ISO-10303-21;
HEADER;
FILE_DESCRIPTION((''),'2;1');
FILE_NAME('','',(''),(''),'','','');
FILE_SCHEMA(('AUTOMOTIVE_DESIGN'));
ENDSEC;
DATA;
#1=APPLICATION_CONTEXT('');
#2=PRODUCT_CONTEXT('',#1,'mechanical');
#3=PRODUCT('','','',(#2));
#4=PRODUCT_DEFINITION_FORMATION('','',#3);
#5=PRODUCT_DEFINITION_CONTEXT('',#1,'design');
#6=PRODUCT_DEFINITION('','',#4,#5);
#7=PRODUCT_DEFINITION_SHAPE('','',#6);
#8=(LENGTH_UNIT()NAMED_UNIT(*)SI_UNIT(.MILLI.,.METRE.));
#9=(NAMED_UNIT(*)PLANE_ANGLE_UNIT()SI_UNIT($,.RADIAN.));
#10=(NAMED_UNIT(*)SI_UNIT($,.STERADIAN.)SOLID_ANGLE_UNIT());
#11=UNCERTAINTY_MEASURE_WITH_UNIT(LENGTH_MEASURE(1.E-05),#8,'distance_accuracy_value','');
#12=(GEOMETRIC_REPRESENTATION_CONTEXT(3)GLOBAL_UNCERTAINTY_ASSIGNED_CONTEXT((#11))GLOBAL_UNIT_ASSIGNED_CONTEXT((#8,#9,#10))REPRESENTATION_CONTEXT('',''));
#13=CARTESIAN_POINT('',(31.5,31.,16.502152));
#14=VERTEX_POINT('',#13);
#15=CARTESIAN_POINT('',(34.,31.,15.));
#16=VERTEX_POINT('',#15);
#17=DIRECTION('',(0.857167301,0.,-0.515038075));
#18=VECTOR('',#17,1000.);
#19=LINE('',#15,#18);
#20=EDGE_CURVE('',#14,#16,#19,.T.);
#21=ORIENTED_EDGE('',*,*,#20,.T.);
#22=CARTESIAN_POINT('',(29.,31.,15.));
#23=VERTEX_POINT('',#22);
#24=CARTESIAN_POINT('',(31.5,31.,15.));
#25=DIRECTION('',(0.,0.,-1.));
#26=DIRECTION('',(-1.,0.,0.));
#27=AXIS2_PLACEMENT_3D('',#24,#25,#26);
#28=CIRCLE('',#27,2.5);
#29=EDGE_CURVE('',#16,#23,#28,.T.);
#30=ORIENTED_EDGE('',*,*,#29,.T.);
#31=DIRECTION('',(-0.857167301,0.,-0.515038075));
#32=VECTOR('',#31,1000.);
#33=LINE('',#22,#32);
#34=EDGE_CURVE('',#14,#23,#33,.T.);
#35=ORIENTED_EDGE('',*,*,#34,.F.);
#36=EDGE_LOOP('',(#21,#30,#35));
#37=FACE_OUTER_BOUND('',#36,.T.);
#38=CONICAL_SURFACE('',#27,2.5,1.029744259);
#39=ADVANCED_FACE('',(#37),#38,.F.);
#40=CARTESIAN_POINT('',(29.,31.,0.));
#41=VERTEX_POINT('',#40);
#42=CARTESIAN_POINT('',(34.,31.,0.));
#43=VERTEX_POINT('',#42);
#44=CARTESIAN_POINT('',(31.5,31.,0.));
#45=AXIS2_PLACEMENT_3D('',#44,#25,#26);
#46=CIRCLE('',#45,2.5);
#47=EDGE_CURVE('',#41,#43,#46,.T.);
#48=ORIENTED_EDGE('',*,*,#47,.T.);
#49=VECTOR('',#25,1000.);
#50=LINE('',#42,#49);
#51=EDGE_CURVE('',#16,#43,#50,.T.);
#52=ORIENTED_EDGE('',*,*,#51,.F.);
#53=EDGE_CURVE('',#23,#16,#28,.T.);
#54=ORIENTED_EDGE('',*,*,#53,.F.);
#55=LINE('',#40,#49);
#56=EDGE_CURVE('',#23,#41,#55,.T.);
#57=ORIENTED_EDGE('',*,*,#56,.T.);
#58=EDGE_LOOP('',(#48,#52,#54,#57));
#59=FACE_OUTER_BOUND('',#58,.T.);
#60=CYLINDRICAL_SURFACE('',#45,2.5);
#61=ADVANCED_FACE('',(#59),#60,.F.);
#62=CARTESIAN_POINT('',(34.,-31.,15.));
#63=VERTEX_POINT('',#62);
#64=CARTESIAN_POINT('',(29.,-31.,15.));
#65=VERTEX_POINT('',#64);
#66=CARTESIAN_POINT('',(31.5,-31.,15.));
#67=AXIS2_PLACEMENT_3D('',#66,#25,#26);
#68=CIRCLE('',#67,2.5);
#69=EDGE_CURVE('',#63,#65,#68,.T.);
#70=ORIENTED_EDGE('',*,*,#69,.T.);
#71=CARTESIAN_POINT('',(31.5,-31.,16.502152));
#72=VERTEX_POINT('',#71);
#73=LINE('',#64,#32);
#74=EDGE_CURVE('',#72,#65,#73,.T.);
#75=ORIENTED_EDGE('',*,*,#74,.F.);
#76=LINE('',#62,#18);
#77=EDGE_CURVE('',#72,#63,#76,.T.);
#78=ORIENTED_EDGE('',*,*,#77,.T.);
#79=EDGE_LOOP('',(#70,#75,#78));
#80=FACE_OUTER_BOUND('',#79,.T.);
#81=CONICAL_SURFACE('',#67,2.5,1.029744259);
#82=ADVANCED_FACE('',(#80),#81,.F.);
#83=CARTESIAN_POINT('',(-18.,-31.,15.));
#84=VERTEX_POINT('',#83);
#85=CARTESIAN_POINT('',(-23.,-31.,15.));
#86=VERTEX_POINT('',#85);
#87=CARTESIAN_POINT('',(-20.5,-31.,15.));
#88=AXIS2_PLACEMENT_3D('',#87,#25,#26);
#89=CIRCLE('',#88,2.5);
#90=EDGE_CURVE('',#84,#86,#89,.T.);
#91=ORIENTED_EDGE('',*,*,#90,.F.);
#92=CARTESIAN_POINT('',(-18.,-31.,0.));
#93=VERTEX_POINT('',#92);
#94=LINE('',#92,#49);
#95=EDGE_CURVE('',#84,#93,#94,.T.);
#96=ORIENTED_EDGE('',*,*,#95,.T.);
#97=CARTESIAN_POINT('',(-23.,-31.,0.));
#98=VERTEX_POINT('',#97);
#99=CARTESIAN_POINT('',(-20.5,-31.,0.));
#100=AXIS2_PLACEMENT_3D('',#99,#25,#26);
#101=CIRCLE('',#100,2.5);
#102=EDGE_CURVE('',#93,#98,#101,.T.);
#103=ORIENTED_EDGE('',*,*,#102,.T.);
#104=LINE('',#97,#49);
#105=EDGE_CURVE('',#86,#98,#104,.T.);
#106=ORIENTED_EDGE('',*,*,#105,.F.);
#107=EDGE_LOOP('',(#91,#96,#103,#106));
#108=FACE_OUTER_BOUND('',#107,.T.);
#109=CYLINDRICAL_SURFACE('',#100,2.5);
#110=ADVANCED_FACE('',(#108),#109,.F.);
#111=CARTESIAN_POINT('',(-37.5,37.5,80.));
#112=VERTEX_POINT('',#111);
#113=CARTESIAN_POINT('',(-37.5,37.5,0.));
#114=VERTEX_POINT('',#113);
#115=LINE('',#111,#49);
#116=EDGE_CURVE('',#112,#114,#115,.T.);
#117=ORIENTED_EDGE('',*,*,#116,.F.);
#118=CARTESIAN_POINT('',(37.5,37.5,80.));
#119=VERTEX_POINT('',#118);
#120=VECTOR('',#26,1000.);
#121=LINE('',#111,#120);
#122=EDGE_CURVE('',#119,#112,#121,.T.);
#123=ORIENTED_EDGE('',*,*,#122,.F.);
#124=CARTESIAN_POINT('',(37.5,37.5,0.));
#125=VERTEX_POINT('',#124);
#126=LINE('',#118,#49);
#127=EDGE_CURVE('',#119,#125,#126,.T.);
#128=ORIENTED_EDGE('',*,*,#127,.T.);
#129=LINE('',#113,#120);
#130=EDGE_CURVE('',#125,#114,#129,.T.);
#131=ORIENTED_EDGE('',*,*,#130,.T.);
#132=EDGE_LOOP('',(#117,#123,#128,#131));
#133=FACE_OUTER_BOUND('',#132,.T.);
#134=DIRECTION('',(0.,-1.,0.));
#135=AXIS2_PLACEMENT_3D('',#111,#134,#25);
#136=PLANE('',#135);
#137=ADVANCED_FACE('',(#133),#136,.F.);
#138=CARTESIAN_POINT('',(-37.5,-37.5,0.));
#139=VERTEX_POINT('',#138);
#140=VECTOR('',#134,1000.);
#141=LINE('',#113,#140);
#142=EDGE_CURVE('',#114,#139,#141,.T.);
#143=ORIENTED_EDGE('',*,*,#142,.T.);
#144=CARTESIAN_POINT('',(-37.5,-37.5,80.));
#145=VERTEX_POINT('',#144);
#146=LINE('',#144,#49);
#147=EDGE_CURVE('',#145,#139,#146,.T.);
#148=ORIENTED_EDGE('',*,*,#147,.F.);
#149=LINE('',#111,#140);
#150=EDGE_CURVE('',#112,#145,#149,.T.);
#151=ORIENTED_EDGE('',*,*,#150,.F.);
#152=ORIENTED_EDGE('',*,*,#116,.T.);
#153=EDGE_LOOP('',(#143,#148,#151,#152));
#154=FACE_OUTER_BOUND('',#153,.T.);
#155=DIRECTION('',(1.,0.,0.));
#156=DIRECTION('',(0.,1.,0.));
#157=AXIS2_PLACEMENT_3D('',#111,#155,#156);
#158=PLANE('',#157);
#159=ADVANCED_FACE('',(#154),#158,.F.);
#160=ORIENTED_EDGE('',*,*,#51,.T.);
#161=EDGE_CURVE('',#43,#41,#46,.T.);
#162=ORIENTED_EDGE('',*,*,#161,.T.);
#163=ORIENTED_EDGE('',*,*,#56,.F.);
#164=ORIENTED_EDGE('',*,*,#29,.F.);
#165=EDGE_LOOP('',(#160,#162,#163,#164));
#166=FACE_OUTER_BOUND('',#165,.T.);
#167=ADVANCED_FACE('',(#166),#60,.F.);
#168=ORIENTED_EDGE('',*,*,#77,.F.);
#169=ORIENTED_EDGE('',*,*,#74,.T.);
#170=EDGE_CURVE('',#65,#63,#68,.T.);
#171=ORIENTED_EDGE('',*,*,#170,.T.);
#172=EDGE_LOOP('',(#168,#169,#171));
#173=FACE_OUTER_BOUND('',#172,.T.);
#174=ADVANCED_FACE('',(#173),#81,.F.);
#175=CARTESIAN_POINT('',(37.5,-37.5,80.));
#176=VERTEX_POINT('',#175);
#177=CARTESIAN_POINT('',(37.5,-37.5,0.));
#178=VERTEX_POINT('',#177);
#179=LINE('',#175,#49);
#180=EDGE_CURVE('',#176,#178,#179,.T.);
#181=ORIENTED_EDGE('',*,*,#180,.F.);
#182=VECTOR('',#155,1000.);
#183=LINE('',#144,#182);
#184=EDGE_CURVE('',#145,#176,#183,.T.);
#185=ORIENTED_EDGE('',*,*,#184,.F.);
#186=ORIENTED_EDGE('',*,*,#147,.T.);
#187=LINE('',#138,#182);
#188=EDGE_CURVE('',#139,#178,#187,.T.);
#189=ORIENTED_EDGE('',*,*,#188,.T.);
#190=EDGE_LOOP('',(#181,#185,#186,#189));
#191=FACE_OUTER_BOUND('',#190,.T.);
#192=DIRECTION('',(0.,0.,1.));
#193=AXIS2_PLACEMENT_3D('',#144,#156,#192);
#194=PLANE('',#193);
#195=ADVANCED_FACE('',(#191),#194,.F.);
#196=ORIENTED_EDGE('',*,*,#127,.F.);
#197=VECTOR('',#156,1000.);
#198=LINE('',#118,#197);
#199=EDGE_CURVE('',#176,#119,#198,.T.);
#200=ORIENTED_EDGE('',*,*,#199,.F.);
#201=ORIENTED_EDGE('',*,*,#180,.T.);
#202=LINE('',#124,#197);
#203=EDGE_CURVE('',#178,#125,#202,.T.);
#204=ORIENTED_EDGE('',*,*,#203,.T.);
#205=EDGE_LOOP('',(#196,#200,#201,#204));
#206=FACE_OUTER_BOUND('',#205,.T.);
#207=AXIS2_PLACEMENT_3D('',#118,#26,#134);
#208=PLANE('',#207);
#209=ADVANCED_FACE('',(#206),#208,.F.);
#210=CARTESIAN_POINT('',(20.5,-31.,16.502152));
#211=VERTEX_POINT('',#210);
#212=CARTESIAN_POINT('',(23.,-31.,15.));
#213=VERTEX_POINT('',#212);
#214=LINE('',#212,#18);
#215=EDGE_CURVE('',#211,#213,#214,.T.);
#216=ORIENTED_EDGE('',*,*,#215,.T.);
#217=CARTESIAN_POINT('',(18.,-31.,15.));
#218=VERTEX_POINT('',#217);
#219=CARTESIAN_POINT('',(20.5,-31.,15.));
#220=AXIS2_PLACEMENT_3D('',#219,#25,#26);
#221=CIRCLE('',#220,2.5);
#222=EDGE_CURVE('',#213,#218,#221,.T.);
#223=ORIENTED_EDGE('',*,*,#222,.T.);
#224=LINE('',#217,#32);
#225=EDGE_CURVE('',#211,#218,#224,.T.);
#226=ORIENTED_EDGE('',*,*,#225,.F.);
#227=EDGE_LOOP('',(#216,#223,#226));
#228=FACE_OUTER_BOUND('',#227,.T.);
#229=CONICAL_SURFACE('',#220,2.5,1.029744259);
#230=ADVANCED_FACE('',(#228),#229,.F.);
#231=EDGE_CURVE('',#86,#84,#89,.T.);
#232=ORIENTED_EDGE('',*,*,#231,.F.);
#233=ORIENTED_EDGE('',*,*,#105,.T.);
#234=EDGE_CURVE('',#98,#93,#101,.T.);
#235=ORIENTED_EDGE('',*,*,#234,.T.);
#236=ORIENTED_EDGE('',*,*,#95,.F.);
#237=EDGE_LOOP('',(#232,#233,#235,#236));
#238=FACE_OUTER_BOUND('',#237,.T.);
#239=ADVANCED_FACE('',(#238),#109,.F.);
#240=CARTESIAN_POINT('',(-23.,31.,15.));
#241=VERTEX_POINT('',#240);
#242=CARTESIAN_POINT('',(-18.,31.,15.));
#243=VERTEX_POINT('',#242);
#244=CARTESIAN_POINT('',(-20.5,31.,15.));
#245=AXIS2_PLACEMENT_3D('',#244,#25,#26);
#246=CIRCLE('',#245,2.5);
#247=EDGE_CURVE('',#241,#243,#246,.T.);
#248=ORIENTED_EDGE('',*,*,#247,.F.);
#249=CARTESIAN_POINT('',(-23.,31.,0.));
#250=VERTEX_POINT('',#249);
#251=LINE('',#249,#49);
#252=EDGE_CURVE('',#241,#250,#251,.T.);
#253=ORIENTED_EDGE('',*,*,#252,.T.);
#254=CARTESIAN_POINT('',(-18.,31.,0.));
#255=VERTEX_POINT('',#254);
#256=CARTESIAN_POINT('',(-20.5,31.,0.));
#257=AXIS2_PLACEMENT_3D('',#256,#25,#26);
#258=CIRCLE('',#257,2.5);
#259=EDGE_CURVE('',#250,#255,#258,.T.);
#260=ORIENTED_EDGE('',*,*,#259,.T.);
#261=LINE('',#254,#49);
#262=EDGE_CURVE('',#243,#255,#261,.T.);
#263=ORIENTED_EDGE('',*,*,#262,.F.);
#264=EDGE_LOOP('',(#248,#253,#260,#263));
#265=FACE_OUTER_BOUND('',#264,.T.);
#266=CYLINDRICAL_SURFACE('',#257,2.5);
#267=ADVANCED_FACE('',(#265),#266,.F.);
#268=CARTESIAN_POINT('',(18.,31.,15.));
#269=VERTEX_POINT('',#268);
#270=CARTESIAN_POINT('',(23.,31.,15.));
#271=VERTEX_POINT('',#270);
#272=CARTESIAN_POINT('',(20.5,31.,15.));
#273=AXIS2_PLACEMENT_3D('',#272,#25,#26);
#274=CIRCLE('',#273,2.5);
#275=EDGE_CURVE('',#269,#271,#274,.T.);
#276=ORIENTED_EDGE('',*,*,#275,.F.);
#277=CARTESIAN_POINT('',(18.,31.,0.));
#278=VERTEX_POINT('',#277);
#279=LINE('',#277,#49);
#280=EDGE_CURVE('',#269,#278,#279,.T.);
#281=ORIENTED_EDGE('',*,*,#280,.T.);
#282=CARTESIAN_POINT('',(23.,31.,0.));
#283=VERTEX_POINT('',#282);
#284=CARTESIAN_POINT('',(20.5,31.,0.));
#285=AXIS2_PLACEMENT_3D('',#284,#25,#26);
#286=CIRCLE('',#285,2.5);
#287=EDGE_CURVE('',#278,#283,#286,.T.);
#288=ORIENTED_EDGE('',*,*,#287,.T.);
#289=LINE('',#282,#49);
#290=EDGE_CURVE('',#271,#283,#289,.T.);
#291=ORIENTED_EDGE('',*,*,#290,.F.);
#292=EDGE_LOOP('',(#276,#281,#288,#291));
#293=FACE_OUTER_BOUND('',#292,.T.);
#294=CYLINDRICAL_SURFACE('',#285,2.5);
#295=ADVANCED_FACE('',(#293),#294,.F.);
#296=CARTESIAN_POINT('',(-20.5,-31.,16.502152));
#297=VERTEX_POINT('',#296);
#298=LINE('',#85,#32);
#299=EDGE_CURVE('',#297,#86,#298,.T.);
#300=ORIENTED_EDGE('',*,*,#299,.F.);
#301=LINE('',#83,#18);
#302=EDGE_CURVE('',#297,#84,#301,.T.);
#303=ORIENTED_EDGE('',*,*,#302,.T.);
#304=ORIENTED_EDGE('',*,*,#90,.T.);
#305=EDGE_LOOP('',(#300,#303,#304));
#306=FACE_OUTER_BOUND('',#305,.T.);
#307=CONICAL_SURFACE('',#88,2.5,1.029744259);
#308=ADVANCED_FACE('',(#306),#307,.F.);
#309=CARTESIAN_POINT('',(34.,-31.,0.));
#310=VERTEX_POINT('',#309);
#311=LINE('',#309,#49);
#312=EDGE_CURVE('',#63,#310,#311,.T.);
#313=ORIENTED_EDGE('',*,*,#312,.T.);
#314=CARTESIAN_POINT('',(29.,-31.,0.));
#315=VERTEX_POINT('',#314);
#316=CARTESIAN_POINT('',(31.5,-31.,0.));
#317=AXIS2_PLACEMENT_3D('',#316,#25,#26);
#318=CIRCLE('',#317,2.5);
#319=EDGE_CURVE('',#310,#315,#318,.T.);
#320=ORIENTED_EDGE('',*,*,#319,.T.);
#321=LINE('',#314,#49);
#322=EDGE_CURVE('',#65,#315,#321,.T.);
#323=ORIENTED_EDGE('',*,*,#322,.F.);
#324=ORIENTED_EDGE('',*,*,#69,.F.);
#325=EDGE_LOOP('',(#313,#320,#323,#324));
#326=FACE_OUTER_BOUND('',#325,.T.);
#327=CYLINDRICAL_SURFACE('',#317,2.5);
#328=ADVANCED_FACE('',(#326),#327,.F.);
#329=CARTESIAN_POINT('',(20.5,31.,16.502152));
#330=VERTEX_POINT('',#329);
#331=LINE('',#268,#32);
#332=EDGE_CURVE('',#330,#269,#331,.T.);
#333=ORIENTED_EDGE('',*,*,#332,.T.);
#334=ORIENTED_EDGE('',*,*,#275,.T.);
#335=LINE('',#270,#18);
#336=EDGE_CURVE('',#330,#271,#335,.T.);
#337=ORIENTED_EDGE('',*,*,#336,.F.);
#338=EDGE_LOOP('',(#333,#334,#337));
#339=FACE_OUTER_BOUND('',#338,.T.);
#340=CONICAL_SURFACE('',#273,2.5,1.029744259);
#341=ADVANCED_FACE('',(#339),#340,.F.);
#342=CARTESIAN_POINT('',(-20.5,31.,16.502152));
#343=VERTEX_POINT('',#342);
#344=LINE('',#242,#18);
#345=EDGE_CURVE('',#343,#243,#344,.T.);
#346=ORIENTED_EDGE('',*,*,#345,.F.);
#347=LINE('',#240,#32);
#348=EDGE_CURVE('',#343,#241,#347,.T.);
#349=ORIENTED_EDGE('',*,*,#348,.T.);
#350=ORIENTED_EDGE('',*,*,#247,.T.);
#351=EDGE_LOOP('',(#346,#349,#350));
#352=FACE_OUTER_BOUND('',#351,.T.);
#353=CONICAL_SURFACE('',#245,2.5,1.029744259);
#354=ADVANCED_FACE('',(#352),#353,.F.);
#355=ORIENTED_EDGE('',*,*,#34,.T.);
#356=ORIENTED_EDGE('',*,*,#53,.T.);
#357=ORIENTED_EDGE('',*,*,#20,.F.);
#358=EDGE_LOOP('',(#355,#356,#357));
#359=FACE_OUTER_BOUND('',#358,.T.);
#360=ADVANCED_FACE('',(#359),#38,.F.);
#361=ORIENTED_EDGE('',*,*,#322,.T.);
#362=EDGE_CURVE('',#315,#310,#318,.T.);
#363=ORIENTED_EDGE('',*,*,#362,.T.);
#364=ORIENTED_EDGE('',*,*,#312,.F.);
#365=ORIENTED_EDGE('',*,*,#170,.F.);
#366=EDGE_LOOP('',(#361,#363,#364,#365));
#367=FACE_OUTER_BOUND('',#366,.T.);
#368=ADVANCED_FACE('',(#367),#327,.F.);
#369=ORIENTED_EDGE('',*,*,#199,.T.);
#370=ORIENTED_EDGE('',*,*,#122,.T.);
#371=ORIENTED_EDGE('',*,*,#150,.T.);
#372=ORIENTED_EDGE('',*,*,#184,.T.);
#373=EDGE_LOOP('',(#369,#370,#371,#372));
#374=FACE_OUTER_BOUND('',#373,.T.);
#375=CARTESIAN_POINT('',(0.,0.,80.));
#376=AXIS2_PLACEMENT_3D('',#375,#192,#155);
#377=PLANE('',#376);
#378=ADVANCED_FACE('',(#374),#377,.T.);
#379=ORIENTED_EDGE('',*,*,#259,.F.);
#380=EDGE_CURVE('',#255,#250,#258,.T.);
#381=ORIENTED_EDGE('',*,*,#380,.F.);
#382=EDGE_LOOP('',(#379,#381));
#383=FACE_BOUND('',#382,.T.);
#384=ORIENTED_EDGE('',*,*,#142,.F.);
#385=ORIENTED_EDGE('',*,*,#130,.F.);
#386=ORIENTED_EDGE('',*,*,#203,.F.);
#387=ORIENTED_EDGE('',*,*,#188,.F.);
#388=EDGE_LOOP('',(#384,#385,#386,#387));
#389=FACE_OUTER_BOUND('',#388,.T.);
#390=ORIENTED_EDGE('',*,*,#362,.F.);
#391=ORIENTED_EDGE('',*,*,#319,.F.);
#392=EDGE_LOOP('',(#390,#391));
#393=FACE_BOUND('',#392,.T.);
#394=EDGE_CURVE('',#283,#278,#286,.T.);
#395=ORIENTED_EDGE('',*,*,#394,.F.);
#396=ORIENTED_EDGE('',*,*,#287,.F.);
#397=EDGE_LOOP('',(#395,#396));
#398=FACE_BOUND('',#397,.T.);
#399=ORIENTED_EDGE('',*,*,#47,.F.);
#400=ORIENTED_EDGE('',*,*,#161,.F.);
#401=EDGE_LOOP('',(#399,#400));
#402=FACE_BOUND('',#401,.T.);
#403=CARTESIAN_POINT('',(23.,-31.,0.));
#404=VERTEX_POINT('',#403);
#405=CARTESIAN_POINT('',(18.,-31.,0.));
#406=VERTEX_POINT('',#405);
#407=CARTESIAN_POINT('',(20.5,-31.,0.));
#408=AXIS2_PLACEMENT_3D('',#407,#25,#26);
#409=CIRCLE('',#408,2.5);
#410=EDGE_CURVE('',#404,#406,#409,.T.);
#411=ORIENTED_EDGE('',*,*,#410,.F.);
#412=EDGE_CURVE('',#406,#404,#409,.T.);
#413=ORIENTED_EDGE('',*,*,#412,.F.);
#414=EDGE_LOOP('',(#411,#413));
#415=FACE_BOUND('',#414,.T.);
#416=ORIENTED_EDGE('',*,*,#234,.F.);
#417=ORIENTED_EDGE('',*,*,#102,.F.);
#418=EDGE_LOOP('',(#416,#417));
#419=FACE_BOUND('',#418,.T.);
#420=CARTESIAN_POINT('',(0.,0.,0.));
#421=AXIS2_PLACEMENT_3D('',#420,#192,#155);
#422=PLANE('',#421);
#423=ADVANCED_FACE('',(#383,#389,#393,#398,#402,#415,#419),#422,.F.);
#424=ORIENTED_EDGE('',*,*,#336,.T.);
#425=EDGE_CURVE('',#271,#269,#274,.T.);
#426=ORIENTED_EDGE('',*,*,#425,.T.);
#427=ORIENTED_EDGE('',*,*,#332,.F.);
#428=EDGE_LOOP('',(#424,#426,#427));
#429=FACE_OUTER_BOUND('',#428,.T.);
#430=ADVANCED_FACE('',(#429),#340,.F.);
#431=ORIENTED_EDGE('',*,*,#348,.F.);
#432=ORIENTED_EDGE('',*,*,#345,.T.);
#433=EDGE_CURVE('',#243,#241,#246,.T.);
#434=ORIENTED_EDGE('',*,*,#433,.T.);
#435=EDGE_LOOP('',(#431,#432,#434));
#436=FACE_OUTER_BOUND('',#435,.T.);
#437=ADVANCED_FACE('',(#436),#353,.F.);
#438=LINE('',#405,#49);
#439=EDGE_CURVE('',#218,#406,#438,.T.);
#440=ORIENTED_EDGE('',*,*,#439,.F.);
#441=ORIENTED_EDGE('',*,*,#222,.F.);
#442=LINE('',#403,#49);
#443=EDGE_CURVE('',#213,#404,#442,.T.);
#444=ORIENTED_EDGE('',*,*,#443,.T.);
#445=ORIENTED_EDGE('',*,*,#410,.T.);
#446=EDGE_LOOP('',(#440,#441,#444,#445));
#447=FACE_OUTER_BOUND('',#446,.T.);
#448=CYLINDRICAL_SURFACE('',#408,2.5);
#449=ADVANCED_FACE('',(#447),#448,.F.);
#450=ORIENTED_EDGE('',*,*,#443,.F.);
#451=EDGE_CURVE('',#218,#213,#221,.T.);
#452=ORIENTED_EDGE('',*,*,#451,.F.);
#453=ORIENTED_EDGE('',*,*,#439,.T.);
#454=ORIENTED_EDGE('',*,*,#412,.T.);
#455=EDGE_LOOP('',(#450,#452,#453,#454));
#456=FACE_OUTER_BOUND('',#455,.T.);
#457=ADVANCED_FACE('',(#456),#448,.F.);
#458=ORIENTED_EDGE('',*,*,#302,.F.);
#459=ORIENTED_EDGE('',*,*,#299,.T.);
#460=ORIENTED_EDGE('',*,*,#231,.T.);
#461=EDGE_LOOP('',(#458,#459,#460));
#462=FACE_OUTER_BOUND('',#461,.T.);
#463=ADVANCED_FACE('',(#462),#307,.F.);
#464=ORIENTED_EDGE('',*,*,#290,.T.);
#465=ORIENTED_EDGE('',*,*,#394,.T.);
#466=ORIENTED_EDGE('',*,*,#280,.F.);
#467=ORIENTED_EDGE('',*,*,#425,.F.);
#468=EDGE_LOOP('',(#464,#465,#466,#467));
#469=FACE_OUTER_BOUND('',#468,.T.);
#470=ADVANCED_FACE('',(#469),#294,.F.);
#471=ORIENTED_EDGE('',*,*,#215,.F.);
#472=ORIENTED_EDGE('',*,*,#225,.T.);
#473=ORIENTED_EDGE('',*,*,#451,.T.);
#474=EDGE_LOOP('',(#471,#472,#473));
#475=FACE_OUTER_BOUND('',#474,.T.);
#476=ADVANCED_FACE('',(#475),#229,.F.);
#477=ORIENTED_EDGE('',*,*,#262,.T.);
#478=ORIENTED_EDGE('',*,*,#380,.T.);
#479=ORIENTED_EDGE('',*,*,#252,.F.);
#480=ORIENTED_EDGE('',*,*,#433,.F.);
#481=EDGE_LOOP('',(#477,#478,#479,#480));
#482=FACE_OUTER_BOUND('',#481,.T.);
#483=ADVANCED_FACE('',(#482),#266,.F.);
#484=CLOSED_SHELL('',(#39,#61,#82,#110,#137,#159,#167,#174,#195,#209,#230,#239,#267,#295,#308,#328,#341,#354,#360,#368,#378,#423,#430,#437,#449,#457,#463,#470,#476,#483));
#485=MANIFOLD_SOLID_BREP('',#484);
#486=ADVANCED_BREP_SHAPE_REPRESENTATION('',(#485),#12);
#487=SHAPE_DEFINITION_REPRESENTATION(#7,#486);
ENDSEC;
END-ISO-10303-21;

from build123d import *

# Parameters (mm, degrees)
SKETCH_1_W             = 75
SKETCH_1_H             = 75
EXTRUDE_1_DEPTH        = 80
HOLE_WIZARD_M6_2_D     = 5
HOLE_WIZARD_M6_2_DEPTH = 15
HOLE_WIZARD_M6_2_TIP   = 1.502151548


with BuildPart() as part:
    # 草图1 → 凸台-拉伸1 (new body)
    with BuildSketch(Plane.XY):
        Rectangle(SKETCH_1_W, SKETCH_1_H)
    extrude(amount=EXTRUDE_1_DEPTH)

    # M6 螺纹孔2
    with Locations(Plane(origin=(0, 0, 0), x_dir=(-1, 0, 0), z_dir=(0, 0, -1))):
        with Locations((-31.5, 31), (-20.5, 31), (20.5, 31), (20.5, -31), (-20.5, -31), (-31.5, -31)):
            Hole(HOLE_WIZARD_M6_2_D / 2, depth=HOLE_WIZARD_M6_2_DEPTH)
            with Locations((0, 0, -(HOLE_WIZARD_M6_2_DEPTH + HOLE_WIZARD_M6_2_TIP / 2))):  # 118° drill point
                Cone(0, HOLE_WIZARD_M6_2_D / 2, HOLE_WIZARD_M6_2_TIP, mode=Mode.SUBTRACT)


solid = part.part
